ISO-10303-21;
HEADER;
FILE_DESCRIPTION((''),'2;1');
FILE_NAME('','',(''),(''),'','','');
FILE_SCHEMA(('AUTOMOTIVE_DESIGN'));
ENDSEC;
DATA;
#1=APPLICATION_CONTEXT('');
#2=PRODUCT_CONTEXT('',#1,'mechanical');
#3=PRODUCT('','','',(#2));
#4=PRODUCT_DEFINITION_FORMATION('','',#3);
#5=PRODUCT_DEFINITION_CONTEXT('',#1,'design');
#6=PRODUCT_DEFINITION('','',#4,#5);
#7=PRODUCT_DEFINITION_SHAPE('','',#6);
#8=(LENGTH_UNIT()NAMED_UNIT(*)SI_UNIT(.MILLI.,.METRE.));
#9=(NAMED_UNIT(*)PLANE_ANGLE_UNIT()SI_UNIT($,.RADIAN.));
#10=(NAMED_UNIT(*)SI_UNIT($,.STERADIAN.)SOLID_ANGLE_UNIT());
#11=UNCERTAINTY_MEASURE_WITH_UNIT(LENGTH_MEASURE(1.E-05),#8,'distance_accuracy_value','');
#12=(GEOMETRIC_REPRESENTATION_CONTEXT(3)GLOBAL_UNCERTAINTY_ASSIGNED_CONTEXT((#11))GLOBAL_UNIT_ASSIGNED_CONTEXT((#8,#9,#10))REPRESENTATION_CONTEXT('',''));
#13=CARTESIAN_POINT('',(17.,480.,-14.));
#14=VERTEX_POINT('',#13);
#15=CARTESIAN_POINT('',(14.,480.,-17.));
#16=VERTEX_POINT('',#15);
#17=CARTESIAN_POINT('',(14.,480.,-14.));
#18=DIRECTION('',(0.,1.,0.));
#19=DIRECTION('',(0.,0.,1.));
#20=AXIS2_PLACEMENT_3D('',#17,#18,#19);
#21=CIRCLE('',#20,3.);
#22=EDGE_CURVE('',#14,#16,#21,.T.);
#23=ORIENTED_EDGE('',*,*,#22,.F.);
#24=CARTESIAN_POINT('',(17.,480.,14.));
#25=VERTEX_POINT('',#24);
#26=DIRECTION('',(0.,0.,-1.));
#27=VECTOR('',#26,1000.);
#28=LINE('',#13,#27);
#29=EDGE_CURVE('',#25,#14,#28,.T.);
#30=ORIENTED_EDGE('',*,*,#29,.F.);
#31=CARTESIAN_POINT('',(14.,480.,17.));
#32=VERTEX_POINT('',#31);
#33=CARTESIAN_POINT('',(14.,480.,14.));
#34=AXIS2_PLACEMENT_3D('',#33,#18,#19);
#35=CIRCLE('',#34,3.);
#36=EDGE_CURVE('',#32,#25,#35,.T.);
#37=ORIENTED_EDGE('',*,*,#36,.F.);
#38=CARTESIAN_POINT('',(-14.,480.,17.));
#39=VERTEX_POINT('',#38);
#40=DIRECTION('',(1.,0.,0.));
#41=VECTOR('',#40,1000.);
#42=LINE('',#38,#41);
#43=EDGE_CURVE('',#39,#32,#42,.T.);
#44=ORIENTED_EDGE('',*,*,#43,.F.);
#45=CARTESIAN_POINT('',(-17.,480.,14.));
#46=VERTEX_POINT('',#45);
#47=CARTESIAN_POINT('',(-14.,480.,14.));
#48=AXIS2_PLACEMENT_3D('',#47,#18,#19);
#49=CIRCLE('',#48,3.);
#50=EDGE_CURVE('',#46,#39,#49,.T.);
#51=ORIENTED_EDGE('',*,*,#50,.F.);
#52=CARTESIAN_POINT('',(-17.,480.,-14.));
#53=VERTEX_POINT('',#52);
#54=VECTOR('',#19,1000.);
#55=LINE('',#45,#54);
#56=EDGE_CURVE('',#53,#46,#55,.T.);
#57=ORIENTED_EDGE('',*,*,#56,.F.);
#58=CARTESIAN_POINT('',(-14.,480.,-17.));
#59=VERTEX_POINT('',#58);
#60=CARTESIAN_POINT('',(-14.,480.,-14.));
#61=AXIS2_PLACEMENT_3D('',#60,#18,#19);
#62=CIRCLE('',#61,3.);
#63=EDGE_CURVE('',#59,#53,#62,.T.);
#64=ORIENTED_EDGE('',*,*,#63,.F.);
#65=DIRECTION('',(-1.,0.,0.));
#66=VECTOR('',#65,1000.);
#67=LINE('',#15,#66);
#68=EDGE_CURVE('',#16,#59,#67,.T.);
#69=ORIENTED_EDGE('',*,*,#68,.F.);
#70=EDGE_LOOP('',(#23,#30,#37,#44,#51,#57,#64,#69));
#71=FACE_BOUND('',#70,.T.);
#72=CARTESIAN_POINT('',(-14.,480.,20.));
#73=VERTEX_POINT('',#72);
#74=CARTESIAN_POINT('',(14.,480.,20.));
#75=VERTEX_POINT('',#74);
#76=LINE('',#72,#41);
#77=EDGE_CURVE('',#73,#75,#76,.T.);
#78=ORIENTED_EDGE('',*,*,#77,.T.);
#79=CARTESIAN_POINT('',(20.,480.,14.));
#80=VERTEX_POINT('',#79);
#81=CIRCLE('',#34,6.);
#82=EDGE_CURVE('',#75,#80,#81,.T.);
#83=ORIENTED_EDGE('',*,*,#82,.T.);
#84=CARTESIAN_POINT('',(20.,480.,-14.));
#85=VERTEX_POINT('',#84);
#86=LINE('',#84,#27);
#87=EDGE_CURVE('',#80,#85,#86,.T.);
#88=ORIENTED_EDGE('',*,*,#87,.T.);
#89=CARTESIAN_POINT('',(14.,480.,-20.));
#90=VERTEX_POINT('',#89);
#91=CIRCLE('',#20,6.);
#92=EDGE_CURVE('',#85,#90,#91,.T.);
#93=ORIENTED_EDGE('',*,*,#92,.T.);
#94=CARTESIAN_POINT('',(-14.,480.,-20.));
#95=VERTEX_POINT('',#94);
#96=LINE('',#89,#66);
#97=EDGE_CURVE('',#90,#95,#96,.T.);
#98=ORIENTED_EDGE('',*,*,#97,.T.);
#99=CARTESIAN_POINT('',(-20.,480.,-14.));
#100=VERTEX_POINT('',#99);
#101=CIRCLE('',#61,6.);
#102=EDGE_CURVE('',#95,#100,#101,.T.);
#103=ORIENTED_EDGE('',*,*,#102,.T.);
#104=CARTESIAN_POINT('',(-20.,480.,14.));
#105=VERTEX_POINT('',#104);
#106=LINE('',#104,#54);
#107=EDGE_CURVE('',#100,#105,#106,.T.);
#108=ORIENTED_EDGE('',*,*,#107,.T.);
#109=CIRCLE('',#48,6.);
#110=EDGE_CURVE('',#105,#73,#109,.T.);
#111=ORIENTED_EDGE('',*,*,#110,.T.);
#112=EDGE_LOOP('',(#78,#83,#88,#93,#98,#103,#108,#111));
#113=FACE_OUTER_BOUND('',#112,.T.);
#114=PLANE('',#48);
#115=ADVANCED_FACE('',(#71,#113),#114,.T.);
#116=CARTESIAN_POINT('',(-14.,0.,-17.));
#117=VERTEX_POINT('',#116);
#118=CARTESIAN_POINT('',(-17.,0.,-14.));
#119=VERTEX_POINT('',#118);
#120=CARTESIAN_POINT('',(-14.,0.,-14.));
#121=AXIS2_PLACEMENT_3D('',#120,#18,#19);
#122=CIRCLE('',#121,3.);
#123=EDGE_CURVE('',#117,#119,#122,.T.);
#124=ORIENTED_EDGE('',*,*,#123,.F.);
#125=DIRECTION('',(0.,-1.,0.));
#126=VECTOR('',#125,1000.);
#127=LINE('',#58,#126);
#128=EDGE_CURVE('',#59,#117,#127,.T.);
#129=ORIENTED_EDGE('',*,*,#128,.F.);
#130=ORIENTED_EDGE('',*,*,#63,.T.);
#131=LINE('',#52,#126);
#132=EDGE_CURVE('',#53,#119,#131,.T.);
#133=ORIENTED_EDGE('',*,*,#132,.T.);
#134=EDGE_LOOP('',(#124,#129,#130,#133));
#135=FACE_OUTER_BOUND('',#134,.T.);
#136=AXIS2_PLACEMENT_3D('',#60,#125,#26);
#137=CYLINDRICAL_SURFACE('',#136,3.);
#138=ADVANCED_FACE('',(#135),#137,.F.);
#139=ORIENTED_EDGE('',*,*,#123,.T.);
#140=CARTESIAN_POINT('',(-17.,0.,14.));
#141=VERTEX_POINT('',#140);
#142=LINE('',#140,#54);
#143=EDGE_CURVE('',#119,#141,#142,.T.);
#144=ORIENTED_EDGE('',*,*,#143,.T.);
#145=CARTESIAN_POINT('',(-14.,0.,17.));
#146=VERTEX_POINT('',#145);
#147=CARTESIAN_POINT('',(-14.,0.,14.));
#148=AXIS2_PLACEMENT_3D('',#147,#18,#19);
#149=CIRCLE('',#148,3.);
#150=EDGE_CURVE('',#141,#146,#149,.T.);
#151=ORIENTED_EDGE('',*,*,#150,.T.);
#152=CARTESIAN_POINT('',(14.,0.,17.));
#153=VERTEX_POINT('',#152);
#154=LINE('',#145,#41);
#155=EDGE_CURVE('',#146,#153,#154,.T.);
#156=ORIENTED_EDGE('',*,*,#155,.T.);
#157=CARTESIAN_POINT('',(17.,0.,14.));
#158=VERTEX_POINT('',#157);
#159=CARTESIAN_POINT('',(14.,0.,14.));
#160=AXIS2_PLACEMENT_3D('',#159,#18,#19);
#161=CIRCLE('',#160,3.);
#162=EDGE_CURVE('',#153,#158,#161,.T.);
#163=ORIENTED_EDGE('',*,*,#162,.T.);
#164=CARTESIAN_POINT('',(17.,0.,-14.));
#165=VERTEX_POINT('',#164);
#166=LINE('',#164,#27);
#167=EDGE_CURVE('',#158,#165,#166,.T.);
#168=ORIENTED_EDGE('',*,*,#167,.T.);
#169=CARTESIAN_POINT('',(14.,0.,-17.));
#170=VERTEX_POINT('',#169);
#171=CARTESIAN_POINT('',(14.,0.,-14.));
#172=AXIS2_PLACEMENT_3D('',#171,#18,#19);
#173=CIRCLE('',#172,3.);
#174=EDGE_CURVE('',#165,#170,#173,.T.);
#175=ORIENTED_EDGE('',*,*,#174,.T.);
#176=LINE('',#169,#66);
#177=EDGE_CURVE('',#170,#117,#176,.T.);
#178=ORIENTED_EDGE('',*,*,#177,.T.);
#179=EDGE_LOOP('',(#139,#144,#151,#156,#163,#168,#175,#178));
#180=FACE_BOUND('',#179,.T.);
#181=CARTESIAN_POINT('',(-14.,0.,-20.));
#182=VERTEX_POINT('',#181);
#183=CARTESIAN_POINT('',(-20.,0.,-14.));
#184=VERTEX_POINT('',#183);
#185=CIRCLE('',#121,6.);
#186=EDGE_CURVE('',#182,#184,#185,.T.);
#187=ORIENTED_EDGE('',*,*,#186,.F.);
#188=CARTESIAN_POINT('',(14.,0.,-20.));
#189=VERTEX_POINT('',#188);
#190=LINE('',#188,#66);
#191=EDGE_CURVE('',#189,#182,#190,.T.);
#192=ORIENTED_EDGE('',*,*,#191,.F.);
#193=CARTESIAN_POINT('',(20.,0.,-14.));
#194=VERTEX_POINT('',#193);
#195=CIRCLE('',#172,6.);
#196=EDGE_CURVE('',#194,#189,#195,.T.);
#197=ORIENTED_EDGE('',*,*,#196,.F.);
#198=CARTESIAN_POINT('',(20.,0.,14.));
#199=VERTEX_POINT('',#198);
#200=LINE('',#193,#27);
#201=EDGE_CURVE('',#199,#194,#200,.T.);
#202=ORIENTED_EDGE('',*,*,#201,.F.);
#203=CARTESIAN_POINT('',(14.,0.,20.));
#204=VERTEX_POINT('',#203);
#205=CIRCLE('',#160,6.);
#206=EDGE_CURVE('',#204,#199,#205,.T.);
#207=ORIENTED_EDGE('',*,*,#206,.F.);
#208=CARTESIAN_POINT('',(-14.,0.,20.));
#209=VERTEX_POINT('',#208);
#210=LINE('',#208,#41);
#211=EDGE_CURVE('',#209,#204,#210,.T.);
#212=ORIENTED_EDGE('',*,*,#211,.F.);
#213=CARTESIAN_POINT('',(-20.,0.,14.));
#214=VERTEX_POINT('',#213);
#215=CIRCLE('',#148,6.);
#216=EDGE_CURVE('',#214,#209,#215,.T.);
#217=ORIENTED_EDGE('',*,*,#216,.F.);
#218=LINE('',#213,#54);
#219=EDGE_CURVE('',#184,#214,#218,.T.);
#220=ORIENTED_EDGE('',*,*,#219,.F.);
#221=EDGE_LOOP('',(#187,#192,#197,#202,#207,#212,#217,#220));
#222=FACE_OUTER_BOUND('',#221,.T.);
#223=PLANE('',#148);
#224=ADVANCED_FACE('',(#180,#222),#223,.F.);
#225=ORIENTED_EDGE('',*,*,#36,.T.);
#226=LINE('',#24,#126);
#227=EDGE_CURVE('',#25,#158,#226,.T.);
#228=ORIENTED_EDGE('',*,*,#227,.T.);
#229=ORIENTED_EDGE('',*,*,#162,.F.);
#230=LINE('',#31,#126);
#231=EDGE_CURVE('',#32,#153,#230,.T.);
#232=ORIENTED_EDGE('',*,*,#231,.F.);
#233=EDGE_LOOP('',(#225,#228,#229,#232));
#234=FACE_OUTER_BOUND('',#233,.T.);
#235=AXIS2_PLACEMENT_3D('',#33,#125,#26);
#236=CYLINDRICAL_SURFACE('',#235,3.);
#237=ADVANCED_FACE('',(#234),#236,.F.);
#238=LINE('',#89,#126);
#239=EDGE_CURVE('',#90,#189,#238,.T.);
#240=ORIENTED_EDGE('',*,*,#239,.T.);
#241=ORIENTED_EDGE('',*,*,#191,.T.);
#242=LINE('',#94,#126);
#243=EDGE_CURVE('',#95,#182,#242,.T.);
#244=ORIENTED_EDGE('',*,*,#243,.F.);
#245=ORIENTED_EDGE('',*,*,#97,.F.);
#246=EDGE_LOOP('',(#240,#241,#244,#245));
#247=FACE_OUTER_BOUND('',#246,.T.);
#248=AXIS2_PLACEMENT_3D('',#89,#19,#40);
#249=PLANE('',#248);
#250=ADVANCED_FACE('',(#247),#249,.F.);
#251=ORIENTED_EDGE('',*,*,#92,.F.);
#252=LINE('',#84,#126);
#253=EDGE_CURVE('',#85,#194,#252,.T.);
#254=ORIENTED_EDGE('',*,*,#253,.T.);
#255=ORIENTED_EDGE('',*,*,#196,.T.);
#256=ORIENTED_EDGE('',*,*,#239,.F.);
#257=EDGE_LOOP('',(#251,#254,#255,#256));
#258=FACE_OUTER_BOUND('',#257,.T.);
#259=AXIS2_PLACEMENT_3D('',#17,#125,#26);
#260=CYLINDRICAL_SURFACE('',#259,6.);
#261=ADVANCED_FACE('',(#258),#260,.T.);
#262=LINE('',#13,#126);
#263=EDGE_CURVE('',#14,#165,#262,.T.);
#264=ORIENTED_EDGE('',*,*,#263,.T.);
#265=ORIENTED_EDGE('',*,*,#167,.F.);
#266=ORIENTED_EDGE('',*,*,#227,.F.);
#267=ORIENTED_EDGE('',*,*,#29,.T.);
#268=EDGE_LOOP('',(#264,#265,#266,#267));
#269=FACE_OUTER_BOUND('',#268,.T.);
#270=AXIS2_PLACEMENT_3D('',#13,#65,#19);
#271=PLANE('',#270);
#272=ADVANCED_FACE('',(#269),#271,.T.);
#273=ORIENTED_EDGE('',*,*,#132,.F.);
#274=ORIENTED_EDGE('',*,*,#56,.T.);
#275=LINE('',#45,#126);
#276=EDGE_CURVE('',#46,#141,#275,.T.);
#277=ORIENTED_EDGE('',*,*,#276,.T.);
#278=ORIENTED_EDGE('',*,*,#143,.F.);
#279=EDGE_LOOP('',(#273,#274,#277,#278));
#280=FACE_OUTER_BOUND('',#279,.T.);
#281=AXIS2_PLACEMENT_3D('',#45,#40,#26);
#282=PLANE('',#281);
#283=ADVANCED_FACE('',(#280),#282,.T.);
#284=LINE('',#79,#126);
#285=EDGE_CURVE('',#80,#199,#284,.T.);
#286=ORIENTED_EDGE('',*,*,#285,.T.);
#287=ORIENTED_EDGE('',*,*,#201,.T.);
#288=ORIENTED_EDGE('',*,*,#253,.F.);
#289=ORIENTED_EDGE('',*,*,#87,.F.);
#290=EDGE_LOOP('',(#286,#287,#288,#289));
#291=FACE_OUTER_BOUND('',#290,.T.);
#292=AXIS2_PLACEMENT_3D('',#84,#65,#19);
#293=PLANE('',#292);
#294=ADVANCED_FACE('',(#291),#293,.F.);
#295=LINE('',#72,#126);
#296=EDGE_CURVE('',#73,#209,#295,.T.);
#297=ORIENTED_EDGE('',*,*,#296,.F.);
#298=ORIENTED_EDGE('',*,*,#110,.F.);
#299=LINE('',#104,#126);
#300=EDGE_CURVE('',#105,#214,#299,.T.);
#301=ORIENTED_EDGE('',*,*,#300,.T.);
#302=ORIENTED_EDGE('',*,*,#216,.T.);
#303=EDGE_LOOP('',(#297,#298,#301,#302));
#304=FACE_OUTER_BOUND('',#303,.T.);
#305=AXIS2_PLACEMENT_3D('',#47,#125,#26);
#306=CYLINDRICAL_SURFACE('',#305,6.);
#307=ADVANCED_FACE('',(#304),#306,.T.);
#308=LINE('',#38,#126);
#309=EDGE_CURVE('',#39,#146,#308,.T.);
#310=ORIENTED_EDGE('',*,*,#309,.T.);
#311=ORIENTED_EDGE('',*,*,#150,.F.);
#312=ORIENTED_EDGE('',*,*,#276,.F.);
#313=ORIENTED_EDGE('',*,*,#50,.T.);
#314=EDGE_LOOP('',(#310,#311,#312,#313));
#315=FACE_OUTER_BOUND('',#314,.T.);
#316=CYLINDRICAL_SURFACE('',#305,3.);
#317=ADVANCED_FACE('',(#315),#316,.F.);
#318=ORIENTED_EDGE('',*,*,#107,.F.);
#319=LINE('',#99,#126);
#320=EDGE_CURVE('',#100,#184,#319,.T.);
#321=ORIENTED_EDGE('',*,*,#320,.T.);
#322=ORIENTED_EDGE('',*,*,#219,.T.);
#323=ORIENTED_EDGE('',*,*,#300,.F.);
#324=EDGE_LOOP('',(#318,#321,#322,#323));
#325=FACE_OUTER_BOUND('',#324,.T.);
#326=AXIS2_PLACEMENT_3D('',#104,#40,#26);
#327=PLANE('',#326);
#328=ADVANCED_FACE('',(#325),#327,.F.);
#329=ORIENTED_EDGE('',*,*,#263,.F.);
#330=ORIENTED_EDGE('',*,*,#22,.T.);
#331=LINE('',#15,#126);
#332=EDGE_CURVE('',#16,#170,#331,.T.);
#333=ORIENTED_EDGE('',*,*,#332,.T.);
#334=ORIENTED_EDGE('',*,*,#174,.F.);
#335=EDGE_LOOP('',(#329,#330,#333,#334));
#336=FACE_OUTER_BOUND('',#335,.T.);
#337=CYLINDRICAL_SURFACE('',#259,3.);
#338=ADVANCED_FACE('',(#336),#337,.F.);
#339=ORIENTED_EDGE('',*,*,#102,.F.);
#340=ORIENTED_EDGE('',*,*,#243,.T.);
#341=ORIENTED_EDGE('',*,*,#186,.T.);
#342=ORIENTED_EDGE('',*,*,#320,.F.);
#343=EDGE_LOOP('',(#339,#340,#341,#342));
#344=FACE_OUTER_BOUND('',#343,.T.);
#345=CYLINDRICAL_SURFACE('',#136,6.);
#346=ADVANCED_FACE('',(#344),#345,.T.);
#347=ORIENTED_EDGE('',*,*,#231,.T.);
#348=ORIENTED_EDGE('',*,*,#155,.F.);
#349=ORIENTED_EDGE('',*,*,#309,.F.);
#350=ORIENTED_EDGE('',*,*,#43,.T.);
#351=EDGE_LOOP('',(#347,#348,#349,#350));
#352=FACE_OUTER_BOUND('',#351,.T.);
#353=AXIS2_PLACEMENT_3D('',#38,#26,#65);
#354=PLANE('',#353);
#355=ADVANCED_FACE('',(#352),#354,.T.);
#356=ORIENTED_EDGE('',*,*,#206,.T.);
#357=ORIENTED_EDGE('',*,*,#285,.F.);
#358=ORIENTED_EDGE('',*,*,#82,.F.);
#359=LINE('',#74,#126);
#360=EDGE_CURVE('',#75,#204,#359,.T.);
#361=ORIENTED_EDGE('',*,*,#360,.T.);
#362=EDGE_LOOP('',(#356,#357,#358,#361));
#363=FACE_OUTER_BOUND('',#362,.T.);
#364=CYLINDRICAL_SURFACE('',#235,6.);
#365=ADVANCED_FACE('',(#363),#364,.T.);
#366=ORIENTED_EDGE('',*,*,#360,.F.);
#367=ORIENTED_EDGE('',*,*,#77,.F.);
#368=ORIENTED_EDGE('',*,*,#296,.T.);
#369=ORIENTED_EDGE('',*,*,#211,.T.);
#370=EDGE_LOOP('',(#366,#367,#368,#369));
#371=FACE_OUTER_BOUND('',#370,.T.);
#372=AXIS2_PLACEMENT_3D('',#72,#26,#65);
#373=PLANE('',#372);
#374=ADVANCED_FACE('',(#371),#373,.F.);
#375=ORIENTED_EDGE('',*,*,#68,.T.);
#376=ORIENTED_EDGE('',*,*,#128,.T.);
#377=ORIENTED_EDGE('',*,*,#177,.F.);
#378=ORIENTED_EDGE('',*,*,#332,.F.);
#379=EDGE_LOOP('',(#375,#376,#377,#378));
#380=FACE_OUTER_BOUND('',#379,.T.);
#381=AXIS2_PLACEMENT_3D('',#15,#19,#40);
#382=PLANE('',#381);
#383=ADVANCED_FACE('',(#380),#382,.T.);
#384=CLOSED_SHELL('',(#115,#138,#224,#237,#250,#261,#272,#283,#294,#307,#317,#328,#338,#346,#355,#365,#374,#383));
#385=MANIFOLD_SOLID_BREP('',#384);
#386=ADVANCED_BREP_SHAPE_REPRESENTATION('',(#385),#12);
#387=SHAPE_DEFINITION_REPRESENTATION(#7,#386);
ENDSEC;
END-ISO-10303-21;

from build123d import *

# Parameters (mm, degrees)
COLD_FORMED_HOLLOW_SQUARE_STEEL_GB_T672_DEPTH = 480


with BuildPart() as part:
    # Sketch12 → Cold-formed hollow square steel (gb t6728-2002) 40×3-example.com(1) (new body)
    with BuildSketch(Plane(origin=(0, 0, 0), x_dir=(-1, 0, 0), z_dir=(0, 1, 0))):
        with BuildLine():
            Line((-14, -20), (14, -20))
            ThreePointArc((14, -20), (18.242640687, -18.242640687), (20, -14))
            Line((20, -14), (20, 14))
            ThreePointArc((20, 14), (18.242640687, 18.242640687), (14, 20))
            Line((14, 20), (-14, 20))
            ThreePointArc((-14, 20), (-18.242640687, 18.242640687), (-20, 14))
            Line((-20, 14), (-20, -14))
            ThreePointArc((-20, -14), (-18.242640687, -18.242640687), (-14, -20))
        make_face()
        with BuildLine():
            Line((-14, -17), (14, -17))
            ThreePointArc((14, -17), (16.121320344, -16.121320344), (17, -14))
            Line((17, -14), (17, 14))
            ThreePointArc((17, 14), (16.121320344, 16.121320344), (14, 17))
            Line((14, 17), (-14, 17))
            ThreePointArc((-14, 17), (-16.121320344, 16.121320344), (-17, 14))
            Line((-17, 14), (-17, -14))
            ThreePointArc((-17, -14), (-16.121320344, -16.121320344), (-14, -17))
        make_face(mode=Mode.SUBTRACT)
    extrude(amount=COLD_FORMED_HOLLOW_SQUARE_STEEL_GB_T672_DEPTH)


solid = part.part
